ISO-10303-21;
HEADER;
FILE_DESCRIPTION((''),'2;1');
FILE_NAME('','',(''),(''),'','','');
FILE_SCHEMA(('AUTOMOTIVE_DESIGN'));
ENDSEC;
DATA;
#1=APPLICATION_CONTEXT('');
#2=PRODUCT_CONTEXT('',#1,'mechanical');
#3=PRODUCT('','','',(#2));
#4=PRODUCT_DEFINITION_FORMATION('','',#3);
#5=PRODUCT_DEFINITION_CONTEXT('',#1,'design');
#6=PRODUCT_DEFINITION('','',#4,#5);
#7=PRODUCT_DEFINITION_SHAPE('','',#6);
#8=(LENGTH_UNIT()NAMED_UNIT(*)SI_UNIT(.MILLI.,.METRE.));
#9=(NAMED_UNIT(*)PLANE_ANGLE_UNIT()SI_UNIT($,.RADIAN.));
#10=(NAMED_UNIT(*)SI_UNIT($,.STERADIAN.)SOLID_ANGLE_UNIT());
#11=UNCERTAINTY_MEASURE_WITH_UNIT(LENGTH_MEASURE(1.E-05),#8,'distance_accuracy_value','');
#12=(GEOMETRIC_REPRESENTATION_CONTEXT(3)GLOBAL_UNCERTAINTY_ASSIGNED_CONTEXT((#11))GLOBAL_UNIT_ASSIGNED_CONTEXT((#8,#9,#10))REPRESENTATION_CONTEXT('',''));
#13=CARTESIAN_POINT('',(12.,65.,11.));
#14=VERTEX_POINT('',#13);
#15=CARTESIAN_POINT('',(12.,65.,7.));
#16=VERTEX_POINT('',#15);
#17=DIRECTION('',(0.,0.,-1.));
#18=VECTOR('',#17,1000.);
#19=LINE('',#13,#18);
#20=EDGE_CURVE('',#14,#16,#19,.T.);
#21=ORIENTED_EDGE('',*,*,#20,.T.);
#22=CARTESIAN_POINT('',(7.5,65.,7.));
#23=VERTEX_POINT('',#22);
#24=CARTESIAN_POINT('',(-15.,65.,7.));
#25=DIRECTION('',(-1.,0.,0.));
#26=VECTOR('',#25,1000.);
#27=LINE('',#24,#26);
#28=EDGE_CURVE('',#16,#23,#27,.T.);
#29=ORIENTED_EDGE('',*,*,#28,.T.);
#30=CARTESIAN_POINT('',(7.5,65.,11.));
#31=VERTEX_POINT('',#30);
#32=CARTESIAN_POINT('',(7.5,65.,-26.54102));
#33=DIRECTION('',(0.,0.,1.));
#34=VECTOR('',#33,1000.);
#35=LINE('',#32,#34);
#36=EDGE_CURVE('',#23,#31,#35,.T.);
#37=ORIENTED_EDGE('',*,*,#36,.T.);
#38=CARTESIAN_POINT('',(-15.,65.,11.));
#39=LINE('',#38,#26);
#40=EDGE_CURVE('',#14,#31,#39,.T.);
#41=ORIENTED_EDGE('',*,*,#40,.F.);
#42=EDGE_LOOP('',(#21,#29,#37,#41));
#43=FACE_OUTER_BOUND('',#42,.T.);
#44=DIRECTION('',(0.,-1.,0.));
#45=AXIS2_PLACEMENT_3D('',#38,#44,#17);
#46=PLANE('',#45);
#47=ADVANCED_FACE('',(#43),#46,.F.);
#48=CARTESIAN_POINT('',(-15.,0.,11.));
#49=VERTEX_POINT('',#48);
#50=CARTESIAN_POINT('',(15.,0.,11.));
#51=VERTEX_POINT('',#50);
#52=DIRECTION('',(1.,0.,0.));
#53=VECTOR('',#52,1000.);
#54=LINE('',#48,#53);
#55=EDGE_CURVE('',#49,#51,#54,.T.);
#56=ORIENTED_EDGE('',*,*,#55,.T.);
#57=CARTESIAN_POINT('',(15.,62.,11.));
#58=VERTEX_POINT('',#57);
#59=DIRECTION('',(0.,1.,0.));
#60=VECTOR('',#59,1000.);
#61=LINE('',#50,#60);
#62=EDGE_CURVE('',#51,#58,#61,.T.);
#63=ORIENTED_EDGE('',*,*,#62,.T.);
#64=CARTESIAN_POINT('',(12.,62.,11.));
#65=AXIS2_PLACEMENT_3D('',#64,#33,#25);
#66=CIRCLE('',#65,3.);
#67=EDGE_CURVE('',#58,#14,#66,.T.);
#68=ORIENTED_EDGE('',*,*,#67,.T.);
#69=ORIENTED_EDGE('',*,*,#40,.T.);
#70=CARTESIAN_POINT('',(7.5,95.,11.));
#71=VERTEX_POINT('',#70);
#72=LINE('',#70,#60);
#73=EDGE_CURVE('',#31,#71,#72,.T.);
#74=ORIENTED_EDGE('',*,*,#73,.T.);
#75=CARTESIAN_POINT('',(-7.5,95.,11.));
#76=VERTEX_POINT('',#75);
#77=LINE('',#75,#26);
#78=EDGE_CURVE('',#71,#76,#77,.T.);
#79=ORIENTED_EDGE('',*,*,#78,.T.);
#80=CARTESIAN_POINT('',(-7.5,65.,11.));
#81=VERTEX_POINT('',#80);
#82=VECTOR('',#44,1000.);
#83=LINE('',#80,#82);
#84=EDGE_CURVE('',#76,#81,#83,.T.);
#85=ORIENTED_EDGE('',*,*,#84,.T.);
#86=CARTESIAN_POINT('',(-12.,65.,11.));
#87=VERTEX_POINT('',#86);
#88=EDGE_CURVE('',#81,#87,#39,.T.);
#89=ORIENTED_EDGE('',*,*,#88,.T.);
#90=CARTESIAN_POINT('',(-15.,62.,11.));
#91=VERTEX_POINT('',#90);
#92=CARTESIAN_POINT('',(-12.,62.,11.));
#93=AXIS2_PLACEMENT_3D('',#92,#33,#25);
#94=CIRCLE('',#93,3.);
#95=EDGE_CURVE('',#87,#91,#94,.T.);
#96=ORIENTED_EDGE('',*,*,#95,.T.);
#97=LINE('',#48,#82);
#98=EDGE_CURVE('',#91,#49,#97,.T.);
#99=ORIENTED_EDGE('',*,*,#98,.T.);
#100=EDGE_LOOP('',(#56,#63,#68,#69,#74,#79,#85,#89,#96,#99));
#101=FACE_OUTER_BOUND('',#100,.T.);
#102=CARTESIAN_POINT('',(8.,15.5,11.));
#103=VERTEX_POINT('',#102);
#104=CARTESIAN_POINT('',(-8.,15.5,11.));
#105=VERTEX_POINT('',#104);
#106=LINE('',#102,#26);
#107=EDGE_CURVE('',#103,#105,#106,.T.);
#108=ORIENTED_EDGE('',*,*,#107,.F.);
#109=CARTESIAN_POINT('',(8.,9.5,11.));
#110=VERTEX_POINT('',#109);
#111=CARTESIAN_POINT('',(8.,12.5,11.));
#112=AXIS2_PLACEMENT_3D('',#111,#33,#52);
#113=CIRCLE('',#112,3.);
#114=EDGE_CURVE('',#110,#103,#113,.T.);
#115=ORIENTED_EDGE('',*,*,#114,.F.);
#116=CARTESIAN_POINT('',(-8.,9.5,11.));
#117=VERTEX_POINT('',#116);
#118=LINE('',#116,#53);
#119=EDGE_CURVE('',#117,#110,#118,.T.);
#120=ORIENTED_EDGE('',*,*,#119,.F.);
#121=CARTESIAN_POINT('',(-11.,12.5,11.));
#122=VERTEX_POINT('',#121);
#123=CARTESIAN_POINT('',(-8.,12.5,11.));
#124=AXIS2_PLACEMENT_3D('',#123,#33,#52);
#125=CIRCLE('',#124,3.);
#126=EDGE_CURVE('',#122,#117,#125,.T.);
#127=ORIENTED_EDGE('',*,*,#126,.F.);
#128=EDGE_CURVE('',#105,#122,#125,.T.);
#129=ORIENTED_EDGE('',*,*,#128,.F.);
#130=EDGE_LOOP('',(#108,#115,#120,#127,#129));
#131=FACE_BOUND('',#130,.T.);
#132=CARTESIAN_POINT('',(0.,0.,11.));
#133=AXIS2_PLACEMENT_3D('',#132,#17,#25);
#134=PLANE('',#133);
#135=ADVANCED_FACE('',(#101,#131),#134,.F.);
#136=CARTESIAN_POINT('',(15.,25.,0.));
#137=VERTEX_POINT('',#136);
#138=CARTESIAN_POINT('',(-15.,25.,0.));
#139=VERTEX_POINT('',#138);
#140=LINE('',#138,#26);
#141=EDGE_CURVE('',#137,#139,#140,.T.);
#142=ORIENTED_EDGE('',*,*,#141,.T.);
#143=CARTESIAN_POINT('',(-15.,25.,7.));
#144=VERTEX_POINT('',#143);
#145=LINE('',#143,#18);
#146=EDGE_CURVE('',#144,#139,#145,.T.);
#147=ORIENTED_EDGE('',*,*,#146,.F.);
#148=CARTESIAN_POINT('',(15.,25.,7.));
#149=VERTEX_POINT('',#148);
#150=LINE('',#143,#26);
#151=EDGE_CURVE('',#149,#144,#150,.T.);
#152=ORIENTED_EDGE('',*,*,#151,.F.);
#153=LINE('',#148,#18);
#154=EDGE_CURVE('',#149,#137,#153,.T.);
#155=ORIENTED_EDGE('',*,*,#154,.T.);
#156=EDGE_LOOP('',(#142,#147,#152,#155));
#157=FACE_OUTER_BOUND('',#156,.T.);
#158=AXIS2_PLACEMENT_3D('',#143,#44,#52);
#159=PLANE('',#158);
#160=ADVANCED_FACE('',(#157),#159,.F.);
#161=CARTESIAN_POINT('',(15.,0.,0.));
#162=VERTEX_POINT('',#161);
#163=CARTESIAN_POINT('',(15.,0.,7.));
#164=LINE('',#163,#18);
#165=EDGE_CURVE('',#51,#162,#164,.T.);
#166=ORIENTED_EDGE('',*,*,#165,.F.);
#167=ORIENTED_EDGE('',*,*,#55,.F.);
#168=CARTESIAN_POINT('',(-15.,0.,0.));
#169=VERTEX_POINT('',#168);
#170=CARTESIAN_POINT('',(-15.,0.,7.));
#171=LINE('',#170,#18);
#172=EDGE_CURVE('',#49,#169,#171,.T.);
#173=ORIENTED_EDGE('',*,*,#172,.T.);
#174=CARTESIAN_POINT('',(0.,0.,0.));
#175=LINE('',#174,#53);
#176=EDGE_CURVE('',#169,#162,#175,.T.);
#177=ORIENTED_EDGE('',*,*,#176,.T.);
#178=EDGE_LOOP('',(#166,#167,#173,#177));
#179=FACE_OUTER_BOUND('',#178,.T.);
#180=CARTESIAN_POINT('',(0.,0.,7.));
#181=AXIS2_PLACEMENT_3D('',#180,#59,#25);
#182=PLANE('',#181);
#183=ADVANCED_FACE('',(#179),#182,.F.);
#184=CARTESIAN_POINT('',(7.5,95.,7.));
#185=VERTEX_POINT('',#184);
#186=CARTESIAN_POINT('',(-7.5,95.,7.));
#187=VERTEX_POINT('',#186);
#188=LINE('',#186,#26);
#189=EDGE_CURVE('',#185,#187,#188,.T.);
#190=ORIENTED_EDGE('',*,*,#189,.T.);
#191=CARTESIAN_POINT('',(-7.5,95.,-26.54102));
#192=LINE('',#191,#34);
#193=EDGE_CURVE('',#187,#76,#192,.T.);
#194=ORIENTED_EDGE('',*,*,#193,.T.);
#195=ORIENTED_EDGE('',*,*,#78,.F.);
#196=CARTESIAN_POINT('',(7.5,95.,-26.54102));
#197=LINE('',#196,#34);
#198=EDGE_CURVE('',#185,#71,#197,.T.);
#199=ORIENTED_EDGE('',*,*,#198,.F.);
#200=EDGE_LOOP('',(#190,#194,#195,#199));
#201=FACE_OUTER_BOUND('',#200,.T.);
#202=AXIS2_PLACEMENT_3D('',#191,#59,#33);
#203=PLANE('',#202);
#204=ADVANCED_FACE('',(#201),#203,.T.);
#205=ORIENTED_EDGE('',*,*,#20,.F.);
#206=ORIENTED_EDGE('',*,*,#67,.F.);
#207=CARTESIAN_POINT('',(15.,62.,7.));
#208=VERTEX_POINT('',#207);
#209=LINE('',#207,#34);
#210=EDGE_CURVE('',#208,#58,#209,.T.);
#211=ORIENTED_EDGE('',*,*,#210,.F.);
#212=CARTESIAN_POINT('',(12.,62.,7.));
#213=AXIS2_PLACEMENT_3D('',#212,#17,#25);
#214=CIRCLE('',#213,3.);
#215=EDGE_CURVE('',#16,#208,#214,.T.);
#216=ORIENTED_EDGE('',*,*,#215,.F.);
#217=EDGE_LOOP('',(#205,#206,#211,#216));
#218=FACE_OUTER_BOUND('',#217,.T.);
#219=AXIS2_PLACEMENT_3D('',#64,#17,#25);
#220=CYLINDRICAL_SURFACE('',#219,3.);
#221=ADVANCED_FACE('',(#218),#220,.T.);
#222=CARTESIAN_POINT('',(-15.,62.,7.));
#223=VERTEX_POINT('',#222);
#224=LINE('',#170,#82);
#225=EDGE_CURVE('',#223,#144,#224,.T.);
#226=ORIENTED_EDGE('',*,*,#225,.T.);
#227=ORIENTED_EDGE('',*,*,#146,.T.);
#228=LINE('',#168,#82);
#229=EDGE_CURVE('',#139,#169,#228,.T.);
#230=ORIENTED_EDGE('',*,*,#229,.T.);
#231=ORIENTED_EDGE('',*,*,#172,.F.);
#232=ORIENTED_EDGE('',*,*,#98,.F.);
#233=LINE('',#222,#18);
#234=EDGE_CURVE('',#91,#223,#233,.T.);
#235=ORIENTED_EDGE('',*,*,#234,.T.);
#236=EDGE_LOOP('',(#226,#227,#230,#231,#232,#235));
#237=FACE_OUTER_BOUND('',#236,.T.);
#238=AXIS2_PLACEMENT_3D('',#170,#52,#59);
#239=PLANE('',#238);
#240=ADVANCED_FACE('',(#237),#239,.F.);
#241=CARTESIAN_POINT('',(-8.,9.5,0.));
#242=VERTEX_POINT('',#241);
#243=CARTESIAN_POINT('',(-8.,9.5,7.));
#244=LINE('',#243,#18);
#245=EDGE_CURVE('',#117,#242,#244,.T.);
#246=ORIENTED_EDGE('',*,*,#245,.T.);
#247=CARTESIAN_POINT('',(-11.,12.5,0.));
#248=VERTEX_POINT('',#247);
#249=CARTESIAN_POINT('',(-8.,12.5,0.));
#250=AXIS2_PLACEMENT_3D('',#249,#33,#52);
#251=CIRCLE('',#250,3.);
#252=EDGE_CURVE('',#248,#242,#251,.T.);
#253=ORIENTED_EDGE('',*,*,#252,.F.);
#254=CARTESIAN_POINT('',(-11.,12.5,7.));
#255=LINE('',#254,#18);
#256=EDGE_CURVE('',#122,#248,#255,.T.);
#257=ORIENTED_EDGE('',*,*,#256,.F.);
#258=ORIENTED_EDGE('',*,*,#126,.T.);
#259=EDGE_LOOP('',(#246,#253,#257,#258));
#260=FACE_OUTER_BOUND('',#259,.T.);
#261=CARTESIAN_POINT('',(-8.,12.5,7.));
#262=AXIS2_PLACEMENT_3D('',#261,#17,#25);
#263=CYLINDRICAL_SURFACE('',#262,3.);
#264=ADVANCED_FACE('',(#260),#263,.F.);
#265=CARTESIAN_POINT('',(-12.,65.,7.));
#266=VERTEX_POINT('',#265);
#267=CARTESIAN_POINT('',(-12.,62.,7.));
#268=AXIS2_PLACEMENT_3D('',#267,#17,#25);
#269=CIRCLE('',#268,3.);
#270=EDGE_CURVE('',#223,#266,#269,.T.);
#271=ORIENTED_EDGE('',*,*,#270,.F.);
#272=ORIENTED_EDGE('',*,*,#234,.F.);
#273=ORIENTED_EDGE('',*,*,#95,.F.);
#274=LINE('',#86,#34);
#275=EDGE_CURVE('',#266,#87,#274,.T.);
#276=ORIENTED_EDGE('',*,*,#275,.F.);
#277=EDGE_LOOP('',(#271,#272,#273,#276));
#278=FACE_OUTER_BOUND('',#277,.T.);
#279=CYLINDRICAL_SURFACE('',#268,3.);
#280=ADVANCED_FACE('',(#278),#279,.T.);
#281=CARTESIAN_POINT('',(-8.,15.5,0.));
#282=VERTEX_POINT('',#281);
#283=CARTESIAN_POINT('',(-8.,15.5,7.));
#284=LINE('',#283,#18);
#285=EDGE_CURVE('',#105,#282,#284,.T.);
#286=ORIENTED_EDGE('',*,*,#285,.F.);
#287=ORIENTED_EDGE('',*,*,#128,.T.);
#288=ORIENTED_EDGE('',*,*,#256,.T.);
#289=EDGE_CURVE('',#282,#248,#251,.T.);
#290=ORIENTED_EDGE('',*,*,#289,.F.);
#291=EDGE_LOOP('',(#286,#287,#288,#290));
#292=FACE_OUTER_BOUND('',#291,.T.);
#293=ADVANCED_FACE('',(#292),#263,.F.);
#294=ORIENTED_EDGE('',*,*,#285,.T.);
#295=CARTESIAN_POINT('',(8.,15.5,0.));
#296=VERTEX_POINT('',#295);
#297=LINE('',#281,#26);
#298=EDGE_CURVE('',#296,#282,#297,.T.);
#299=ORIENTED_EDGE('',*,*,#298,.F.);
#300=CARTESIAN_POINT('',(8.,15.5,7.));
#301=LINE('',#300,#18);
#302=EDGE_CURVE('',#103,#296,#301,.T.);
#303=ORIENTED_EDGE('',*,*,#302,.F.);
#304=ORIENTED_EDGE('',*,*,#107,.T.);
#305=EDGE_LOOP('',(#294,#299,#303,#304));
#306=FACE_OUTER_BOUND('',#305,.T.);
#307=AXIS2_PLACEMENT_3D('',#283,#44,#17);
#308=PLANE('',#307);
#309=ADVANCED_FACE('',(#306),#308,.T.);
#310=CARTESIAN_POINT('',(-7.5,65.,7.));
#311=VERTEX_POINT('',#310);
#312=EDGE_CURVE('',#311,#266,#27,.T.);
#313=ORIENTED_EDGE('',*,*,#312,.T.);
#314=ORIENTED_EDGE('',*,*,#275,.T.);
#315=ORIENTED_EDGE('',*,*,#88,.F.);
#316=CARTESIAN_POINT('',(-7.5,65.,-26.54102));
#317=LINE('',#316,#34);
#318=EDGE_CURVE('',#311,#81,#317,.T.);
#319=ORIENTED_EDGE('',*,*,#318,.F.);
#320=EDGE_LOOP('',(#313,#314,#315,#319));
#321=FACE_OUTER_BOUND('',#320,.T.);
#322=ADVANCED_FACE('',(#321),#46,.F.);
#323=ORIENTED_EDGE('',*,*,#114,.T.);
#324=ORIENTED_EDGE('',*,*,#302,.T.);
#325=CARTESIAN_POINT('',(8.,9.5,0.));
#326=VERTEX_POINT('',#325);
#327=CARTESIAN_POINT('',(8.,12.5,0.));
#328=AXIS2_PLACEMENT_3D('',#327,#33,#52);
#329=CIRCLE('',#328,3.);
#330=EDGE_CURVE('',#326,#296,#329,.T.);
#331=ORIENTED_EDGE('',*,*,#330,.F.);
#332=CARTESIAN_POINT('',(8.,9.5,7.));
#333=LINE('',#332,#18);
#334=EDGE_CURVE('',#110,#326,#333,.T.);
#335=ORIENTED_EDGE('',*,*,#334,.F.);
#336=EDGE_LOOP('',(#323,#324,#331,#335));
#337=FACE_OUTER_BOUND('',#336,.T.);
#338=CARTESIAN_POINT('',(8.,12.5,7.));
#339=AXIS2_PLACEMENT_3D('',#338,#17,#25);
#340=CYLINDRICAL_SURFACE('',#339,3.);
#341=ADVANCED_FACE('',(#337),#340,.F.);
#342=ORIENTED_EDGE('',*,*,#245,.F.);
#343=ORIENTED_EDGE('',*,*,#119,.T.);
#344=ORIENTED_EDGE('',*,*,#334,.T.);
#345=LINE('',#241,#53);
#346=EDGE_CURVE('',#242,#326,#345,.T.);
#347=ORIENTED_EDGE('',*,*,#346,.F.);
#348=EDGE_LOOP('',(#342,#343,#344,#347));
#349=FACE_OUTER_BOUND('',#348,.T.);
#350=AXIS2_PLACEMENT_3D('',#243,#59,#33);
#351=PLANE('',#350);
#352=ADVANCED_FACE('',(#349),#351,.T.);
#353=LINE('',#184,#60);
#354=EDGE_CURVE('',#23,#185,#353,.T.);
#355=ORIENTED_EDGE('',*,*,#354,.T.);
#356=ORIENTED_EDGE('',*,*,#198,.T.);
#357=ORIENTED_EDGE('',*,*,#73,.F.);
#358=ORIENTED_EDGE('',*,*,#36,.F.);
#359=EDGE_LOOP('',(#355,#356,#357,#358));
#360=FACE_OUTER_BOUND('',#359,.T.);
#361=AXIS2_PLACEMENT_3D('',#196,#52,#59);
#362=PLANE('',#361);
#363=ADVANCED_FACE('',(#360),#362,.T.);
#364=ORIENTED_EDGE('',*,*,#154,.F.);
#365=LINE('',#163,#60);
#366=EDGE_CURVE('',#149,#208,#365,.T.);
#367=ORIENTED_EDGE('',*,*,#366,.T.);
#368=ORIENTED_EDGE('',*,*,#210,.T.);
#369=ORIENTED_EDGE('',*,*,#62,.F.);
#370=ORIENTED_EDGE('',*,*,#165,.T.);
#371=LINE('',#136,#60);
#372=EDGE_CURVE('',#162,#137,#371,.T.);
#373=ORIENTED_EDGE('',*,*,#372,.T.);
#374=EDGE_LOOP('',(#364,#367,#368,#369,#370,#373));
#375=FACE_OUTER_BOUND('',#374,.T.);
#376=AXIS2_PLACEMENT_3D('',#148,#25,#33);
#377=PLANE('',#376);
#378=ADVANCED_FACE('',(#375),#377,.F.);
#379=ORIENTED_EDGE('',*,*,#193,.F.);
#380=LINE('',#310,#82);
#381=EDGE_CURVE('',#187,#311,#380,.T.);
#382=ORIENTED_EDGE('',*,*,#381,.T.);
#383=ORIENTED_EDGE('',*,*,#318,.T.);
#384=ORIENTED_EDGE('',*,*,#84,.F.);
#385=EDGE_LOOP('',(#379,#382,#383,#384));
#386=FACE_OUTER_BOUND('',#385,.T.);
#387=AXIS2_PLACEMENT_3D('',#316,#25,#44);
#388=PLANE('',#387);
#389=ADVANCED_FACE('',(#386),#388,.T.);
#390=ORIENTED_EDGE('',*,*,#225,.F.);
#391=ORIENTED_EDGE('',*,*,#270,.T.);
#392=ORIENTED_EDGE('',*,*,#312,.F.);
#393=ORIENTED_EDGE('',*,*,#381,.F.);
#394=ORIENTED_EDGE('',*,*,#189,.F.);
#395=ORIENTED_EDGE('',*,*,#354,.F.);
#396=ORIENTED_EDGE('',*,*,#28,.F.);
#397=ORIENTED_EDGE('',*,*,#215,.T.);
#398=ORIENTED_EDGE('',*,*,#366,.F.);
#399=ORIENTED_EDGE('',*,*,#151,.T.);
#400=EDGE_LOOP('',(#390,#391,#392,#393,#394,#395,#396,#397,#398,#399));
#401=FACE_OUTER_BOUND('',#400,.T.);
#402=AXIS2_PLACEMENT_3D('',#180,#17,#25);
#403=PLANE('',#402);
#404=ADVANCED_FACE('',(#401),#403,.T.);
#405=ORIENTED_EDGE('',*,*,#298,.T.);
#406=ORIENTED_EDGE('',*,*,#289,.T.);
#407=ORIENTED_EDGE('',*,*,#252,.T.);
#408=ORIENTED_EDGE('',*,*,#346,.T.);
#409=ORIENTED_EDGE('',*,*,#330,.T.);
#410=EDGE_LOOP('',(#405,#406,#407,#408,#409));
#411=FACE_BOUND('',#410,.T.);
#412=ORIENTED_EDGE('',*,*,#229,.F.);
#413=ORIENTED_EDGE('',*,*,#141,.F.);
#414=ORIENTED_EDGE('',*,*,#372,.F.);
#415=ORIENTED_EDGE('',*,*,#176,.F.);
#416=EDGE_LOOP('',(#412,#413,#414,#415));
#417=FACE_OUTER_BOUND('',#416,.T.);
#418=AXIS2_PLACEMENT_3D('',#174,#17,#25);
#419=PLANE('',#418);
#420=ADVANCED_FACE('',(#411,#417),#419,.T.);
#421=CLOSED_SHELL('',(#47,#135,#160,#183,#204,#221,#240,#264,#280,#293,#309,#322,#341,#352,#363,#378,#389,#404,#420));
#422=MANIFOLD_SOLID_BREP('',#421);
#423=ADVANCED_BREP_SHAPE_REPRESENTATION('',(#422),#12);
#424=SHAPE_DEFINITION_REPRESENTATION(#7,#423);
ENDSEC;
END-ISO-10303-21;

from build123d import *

# Parameters (mm, degrees)
EXTRUDE_1_DEPTH = 7
SKETCH_2_W      = 30
SKETCH_2_H      = 65
EXTRUDE_2_DEPTH = 4
FILLET_1_R      = 3
SKETCH_3_W      = 15
SKETCH_3_H      = 30
EXTRUDE_3_DEPTH = 4


with BuildPart() as part:
    # 草图1 → 凸台-拉伸1 (new body)
    with BuildSketch(Plane.XY):
        Polygon((0, 0), (-15, 0), (-15, 25), (15, 25), (15, 0), align=None)
        with BuildLine():
            Line((-8, 15.5), (8, 15.5))
            ThreePointArc((8, 15.5), (11, 12.5), (8, 9.5))
            Line((8, 9.5), (-8, 9.5))
            ThreePointArc((-8, 9.5), (-11, 12.5), (-8, 15.5))
        make_face(mode=Mode.SUBTRACT)
    extrude(amount=EXTRUDE_1_DEPTH)

    # 草图2 → 凸台-拉伸2 (add)
    with BuildSketch(Plane.XY.offset(7)):
        with Locations((0, 32.5)):
            Rectangle(SKETCH_2_W, SKETCH_2_H)
        with BuildLine():
            Line((-8, 9.5), (8, 9.5))
            ThreePointArc((8, 9.5), (11, 12.5), (8, 15.5))
            Line((8, 15.5), (-8, 15.5))
            ThreePointArc((-8, 15.5), (-11, 12.5), (-8, 9.5))
        make_face(mode=Mode.SUBTRACT)
    extrude(amount=EXTRUDE_2_DEPTH)

    # 圆角1
    fillet_1_edges = [part.edges().sort_by_distance(p)[0] for p in [
        (-15, 65, 9),
        (15, 65, 9),
    ]]
    fillet(fillet_1_edges, radius=FILLET_1_R)

    # 草图3 → 凸台-拉伸3 (add)
    with BuildSketch(Plane.XY.offset(11)):
        with Locations((0, 80)):
            Rectangle(SKETCH_3_W, SKETCH_3_H)
    extrude(amount=-EXTRUDE_3_DEPTH)


solid = part.part
